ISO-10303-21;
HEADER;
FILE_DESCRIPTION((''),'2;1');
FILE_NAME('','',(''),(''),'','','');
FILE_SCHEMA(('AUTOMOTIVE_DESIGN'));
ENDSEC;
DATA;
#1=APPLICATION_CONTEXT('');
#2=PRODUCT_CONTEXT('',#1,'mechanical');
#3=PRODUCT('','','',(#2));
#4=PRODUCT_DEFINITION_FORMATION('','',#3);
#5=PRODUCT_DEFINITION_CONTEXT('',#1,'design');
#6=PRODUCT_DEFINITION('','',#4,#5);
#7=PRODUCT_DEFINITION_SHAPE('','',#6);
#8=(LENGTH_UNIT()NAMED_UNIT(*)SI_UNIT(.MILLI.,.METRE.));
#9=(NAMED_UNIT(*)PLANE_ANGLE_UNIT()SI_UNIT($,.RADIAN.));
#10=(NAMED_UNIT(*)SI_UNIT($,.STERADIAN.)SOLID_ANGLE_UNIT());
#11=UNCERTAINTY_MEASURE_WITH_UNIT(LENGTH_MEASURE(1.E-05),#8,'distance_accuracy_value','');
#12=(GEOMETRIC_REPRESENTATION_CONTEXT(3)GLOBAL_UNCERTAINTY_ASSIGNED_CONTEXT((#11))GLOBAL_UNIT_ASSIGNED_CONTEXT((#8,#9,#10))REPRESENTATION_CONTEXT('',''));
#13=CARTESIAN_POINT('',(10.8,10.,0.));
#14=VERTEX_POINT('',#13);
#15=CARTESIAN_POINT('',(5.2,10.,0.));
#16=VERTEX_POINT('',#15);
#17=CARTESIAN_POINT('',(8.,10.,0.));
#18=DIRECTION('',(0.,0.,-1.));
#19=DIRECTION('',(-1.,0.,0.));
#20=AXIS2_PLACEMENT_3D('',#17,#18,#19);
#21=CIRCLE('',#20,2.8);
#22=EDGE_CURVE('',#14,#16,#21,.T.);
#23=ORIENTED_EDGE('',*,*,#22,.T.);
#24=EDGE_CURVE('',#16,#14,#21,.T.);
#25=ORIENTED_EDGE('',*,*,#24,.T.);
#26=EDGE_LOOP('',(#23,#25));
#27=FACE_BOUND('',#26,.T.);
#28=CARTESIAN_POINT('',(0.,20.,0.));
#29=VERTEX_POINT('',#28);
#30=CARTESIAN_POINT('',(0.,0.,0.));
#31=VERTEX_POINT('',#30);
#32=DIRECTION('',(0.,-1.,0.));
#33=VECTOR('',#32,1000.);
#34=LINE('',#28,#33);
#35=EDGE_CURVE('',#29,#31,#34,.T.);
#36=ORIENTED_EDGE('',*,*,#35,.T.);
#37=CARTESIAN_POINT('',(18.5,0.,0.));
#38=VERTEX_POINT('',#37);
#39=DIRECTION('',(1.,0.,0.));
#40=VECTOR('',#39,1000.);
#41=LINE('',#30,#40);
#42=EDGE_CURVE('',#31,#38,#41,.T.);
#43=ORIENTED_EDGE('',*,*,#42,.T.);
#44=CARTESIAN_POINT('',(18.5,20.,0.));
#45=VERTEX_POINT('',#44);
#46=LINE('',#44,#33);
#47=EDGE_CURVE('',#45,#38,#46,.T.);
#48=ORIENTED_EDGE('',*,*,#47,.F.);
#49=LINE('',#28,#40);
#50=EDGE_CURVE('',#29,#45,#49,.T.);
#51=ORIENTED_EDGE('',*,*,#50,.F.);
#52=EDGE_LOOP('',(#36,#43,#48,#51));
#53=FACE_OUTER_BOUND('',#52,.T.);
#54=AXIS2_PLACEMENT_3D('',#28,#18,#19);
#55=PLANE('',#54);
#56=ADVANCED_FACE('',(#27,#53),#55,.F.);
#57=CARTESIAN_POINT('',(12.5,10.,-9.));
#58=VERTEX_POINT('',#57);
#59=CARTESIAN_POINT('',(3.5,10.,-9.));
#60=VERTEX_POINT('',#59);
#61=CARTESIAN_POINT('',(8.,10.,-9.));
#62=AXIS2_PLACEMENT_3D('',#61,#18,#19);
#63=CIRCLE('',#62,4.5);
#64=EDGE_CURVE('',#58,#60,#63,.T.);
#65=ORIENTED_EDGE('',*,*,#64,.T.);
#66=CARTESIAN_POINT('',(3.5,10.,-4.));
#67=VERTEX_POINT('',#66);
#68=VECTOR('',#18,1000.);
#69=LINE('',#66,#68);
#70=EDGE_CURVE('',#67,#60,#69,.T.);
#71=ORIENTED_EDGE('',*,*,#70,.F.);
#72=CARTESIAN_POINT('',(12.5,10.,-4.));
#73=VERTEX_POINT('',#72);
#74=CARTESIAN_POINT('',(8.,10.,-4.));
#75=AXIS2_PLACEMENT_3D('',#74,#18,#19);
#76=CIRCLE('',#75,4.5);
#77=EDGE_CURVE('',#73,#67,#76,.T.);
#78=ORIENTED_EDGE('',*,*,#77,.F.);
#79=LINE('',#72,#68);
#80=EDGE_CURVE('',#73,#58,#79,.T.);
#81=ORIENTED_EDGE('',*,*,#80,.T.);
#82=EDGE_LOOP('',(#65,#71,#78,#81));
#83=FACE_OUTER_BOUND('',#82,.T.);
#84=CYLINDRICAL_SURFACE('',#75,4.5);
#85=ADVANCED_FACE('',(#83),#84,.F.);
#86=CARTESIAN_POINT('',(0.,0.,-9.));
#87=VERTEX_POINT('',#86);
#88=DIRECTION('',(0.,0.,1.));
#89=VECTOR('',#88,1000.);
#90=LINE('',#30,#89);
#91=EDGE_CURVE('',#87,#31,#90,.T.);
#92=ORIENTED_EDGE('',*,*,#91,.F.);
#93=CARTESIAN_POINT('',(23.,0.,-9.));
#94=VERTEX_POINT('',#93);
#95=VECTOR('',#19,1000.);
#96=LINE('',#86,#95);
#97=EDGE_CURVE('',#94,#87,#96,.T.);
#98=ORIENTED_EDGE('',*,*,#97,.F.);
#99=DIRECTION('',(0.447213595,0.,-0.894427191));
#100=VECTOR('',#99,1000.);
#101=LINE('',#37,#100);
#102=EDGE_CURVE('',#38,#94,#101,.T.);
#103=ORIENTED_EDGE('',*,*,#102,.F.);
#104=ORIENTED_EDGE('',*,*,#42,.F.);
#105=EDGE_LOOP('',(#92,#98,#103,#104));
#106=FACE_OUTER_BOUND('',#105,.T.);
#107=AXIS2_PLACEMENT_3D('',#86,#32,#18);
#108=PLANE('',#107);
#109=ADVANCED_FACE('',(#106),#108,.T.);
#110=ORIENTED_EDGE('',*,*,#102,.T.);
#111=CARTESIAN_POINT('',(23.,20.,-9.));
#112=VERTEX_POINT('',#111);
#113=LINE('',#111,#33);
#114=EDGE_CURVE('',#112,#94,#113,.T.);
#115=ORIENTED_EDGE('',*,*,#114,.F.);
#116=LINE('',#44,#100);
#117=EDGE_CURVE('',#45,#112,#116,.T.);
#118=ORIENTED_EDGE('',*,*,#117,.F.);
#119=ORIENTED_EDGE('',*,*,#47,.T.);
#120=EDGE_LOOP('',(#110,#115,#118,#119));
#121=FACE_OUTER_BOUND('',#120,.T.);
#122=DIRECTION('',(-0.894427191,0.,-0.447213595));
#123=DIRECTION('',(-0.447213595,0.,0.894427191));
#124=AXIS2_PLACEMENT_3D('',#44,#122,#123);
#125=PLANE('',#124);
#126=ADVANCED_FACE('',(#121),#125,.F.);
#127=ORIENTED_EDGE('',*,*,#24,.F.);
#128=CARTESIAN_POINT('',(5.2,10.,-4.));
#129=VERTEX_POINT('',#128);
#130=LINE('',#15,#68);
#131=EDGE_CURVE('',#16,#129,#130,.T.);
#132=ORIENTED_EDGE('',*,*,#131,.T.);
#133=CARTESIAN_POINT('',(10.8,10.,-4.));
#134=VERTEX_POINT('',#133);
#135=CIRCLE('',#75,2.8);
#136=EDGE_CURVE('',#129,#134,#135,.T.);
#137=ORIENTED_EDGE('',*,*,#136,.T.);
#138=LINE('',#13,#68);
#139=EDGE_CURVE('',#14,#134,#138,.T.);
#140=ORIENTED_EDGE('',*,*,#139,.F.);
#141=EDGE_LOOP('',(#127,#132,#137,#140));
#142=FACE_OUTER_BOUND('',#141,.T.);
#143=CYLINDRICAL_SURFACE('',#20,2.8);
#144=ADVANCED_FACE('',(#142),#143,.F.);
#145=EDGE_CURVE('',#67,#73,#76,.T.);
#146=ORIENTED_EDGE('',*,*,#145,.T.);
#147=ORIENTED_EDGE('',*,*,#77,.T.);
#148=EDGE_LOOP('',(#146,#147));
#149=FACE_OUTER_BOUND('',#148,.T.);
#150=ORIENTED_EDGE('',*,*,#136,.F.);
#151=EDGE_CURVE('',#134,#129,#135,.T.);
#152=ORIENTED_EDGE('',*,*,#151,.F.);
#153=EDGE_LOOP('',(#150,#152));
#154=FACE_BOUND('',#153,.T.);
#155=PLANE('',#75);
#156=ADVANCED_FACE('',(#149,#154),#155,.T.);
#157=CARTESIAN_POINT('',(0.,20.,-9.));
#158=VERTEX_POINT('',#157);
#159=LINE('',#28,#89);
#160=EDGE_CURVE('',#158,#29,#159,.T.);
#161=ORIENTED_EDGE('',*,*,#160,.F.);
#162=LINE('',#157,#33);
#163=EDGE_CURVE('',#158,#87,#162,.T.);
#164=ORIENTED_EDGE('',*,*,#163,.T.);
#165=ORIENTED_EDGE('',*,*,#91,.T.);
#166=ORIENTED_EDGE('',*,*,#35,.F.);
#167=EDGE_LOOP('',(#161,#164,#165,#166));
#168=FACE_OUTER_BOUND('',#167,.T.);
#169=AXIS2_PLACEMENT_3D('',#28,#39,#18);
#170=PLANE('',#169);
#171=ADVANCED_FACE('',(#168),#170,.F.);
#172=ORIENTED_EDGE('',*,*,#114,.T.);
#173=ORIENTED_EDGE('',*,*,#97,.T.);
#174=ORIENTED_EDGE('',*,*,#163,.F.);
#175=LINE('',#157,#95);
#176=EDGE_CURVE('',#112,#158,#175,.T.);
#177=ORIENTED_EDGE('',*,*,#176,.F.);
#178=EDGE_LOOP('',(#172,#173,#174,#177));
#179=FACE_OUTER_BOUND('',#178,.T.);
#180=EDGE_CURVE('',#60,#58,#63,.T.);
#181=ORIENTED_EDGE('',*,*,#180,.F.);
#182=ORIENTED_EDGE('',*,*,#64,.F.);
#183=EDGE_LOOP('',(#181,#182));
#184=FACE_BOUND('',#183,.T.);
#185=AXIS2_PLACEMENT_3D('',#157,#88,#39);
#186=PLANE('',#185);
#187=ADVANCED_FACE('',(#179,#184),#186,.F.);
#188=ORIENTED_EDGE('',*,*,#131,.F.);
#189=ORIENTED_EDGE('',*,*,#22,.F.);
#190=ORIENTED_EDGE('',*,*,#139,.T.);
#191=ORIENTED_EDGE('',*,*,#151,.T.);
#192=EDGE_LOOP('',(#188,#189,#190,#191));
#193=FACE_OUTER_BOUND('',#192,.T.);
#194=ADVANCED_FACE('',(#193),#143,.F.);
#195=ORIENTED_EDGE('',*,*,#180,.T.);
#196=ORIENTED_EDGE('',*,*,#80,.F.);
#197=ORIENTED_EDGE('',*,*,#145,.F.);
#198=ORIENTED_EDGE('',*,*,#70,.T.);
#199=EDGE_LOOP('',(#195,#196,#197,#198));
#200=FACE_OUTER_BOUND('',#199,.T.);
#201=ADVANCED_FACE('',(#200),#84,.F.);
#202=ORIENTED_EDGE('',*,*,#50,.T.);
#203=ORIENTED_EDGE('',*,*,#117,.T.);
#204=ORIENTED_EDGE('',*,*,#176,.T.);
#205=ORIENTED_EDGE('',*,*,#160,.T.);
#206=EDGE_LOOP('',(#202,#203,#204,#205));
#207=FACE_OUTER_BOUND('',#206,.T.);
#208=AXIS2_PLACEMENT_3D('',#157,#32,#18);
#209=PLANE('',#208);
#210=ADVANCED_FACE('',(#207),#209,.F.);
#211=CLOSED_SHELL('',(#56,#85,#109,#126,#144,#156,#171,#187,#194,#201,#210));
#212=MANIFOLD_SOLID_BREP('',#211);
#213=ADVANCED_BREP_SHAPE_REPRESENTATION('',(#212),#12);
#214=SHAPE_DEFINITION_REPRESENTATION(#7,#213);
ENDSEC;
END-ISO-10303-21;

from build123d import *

# Parameters (mm, degrees)
EXTRUDE_1_DEPTH     = 20
SKETCH_2_R          = 4.5
CUT_EXTRUDE_1_DEPTH = 5
SKETCH_3_R          = 2.8
CUT_EXTRUDE_2_DEPTH = 31.886890423


with BuildPart() as part:
    # 草图1 → 拉伸1 (new body)
    with BuildSketch(Plane(origin=(0, 0, 0), x_dir=(1, 0, 0), z_dir=(0, 1, 0))):
        Polygon((0, 0), (18.5, 0), (23, 9), (0, 9), align=None)
    extrude(amount=EXTRUDE_1_DEPTH)

    # 草图2 → 切除-拉伸1 (cut)
    with BuildSketch(Plane(origin=(0, 0, -9), x_dir=(-1, 0, 0), z_dir=(0, 0, -1))):
        with Locations((-8, 10)):
            Circle(SKETCH_2_R)
    extrude(amount=-CUT_EXTRUDE_1_DEPTH, mode=Mode.SUBTRACT)

    # 草图3 → 切除-拉伸2 (cut, through all)
    with BuildSketch(Plane(origin=(0, 0, -4), x_dir=(-1, 0, 0), z_dir=(0, 0, -1))):
        with Locations((-8, 10)):
            Circle(SKETCH_3_R)
    extrude(amount=-CUT_EXTRUDE_2_DEPTH, mode=Mode.SUBTRACT)


solid = part.part
